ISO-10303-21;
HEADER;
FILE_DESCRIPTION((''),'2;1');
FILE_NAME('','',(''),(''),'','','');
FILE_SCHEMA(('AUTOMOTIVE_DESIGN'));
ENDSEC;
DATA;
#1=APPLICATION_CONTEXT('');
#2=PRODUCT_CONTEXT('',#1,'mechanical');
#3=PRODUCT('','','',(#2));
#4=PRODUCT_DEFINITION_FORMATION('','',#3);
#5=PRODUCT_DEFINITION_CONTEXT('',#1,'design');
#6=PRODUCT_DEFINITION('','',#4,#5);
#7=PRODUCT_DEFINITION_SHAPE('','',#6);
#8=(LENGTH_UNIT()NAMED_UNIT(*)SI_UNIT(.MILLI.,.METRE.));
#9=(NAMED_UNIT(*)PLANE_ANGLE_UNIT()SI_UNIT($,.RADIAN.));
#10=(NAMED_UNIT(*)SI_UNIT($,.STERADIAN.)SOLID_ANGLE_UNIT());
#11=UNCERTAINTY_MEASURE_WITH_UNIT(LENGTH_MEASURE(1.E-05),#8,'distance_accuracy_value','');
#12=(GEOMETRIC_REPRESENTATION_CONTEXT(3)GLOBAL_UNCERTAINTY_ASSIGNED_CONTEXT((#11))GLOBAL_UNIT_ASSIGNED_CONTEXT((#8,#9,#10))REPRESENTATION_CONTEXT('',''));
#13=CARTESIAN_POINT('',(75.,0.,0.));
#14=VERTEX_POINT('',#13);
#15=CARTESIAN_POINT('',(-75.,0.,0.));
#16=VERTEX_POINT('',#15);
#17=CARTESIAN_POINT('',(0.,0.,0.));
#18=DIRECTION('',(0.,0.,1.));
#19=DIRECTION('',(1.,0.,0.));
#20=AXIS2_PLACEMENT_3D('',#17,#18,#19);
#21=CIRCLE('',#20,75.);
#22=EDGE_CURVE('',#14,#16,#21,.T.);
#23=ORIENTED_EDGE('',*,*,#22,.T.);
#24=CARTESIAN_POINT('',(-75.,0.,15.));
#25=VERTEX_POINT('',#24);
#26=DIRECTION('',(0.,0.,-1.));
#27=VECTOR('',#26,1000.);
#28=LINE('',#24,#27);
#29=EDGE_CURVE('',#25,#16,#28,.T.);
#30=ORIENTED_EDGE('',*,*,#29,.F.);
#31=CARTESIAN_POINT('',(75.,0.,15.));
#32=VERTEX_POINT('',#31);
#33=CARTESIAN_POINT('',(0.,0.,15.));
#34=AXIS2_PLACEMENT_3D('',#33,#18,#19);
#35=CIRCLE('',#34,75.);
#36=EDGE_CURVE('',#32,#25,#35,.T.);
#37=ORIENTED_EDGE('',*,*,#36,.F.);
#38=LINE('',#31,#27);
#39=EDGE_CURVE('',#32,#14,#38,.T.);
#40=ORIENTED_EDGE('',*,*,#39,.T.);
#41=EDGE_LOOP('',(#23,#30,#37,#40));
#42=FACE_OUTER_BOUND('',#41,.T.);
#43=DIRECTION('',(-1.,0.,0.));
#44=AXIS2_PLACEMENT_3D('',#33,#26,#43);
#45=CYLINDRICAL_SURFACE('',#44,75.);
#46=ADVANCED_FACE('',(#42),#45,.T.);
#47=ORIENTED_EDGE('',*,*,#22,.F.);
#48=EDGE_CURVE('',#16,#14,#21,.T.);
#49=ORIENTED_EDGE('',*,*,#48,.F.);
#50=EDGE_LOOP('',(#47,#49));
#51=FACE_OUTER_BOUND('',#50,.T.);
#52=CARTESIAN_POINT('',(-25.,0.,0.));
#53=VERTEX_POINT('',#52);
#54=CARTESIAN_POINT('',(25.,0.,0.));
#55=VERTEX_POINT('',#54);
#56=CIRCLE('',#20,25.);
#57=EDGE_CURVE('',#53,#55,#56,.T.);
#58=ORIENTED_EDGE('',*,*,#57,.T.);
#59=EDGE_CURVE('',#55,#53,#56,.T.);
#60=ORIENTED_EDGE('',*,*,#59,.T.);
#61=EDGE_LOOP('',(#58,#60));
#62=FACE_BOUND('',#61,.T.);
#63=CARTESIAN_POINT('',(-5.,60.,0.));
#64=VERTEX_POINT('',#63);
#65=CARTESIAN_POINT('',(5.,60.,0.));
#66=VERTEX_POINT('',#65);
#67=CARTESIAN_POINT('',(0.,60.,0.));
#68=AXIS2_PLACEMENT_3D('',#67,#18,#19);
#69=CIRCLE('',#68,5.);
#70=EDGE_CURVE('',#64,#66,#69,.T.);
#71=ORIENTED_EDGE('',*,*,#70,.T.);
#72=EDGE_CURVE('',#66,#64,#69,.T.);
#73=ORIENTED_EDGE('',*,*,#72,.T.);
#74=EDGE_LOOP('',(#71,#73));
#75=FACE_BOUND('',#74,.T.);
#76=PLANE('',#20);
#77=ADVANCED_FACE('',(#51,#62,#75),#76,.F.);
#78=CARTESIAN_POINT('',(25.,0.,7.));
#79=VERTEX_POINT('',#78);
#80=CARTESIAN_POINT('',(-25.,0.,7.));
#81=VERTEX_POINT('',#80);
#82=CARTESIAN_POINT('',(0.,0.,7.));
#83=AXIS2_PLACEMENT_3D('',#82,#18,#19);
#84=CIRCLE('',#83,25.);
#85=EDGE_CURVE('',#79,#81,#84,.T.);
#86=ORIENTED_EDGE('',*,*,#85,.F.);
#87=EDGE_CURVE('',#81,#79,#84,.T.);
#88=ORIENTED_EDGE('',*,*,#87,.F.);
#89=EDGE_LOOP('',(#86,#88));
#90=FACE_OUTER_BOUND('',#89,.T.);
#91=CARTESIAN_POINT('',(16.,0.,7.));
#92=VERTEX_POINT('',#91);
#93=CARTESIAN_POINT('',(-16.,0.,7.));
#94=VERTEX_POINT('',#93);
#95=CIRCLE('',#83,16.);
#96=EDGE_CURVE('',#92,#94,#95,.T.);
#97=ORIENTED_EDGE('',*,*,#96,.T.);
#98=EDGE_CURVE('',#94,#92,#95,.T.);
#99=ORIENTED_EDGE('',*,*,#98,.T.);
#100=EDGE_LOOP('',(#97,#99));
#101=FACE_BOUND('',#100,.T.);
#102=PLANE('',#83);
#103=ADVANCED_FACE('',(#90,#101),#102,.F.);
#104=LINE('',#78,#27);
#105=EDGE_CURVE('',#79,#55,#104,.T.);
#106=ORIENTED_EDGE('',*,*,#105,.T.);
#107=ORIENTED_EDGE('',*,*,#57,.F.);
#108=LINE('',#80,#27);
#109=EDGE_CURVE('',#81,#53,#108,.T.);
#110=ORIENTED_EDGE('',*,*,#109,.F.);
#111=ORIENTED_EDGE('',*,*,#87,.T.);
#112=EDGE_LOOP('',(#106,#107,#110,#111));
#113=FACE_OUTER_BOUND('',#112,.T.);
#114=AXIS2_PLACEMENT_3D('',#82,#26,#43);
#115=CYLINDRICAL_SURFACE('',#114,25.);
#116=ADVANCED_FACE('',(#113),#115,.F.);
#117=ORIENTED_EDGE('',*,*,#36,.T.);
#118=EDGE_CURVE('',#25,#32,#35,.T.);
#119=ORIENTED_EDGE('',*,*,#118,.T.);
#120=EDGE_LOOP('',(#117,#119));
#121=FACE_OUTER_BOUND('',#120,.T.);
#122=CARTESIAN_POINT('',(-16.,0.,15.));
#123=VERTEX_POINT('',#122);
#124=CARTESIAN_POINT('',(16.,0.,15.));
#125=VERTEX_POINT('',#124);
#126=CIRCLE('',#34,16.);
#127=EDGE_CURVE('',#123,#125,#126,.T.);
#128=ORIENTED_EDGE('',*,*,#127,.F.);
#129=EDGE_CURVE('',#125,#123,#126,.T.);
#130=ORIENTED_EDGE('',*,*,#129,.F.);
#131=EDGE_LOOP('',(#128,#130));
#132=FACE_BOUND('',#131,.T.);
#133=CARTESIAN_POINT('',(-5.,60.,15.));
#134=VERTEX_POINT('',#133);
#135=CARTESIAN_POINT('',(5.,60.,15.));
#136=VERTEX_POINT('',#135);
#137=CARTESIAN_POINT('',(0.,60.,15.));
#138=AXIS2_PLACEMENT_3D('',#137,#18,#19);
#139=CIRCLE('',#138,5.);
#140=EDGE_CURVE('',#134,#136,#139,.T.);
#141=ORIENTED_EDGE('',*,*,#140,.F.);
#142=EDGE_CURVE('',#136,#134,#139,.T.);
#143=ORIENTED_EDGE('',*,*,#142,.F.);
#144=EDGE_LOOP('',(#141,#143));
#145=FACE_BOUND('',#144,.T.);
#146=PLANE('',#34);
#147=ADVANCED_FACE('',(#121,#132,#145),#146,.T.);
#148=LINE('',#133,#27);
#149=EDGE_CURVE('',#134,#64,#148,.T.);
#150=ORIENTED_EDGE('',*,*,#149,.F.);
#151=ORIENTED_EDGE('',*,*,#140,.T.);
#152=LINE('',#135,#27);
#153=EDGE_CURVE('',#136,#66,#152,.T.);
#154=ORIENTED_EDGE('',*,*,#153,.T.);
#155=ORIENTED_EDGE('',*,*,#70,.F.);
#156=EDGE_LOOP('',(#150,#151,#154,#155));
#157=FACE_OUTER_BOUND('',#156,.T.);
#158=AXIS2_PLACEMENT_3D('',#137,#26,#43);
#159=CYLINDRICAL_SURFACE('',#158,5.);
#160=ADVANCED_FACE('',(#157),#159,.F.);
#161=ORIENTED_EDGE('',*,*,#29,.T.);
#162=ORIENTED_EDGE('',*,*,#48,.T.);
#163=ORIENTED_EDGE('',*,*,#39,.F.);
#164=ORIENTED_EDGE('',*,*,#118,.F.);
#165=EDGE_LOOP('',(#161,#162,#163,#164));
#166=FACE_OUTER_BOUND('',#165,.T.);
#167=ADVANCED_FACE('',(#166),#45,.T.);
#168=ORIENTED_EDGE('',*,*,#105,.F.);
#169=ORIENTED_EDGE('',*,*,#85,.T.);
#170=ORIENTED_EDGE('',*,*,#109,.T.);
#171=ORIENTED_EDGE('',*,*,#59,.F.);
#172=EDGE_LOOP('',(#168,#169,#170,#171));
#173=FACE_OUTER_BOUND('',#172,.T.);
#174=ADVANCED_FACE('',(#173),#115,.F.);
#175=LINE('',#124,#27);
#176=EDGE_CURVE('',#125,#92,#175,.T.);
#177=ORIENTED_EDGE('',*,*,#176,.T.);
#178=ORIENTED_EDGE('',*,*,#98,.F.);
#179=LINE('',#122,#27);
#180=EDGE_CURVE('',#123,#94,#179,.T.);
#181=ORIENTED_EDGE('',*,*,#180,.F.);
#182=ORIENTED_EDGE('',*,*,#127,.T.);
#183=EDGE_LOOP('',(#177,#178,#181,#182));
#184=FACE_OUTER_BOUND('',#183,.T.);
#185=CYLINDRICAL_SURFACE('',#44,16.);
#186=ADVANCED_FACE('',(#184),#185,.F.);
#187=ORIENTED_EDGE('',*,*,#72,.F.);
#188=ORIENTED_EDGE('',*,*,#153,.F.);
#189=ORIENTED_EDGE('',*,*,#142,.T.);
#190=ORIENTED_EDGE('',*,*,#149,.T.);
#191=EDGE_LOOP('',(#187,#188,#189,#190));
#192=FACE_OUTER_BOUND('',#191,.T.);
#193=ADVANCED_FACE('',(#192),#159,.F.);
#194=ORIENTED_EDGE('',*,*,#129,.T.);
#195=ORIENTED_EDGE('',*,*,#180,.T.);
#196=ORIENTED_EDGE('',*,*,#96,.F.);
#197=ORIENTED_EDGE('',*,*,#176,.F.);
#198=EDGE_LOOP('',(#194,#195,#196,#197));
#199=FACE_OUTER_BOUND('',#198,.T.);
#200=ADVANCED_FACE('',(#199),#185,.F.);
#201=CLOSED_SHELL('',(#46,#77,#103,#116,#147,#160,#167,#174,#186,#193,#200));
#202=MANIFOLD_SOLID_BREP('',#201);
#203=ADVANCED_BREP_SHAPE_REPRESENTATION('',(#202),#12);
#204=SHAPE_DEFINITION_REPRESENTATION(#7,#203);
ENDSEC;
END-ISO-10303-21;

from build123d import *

# Parameters (mm, degrees)
SKETCH_1_R          = 75
SKETCH_1_R_2        = 5
SKETCH_1_R_3        = 16
EXTRUDE_1_DEPTH     = 15
CUT_EXTRUDE_START   = -15
SKETCH_2_R          = 25
CUT_EXTRUDE_1_DEPTH = 7


with BuildPart() as part:
    # 草图1 → 凸台-拉伸1 (new body)
    with BuildSketch(Plane.XY):
        Circle(SKETCH_1_R)
        with Locations((0, 60)):
            Circle(SKETCH_1_R_2, mode=Mode.SUBTRACT)
        Circle(SKETCH_1_R_3, mode=Mode.SUBTRACT)
    extrude(amount=EXTRUDE_1_DEPTH)

    # 草图2 → 切除-拉伸1 (cut)
    with BuildSketch(Plane.XY.offset(15).offset(CUT_EXTRUDE_START)):
        Circle(SKETCH_2_R)
    extrude(amount=CUT_EXTRUDE_1_DEPTH, mode=Mode.SUBTRACT)


solid = part.part
